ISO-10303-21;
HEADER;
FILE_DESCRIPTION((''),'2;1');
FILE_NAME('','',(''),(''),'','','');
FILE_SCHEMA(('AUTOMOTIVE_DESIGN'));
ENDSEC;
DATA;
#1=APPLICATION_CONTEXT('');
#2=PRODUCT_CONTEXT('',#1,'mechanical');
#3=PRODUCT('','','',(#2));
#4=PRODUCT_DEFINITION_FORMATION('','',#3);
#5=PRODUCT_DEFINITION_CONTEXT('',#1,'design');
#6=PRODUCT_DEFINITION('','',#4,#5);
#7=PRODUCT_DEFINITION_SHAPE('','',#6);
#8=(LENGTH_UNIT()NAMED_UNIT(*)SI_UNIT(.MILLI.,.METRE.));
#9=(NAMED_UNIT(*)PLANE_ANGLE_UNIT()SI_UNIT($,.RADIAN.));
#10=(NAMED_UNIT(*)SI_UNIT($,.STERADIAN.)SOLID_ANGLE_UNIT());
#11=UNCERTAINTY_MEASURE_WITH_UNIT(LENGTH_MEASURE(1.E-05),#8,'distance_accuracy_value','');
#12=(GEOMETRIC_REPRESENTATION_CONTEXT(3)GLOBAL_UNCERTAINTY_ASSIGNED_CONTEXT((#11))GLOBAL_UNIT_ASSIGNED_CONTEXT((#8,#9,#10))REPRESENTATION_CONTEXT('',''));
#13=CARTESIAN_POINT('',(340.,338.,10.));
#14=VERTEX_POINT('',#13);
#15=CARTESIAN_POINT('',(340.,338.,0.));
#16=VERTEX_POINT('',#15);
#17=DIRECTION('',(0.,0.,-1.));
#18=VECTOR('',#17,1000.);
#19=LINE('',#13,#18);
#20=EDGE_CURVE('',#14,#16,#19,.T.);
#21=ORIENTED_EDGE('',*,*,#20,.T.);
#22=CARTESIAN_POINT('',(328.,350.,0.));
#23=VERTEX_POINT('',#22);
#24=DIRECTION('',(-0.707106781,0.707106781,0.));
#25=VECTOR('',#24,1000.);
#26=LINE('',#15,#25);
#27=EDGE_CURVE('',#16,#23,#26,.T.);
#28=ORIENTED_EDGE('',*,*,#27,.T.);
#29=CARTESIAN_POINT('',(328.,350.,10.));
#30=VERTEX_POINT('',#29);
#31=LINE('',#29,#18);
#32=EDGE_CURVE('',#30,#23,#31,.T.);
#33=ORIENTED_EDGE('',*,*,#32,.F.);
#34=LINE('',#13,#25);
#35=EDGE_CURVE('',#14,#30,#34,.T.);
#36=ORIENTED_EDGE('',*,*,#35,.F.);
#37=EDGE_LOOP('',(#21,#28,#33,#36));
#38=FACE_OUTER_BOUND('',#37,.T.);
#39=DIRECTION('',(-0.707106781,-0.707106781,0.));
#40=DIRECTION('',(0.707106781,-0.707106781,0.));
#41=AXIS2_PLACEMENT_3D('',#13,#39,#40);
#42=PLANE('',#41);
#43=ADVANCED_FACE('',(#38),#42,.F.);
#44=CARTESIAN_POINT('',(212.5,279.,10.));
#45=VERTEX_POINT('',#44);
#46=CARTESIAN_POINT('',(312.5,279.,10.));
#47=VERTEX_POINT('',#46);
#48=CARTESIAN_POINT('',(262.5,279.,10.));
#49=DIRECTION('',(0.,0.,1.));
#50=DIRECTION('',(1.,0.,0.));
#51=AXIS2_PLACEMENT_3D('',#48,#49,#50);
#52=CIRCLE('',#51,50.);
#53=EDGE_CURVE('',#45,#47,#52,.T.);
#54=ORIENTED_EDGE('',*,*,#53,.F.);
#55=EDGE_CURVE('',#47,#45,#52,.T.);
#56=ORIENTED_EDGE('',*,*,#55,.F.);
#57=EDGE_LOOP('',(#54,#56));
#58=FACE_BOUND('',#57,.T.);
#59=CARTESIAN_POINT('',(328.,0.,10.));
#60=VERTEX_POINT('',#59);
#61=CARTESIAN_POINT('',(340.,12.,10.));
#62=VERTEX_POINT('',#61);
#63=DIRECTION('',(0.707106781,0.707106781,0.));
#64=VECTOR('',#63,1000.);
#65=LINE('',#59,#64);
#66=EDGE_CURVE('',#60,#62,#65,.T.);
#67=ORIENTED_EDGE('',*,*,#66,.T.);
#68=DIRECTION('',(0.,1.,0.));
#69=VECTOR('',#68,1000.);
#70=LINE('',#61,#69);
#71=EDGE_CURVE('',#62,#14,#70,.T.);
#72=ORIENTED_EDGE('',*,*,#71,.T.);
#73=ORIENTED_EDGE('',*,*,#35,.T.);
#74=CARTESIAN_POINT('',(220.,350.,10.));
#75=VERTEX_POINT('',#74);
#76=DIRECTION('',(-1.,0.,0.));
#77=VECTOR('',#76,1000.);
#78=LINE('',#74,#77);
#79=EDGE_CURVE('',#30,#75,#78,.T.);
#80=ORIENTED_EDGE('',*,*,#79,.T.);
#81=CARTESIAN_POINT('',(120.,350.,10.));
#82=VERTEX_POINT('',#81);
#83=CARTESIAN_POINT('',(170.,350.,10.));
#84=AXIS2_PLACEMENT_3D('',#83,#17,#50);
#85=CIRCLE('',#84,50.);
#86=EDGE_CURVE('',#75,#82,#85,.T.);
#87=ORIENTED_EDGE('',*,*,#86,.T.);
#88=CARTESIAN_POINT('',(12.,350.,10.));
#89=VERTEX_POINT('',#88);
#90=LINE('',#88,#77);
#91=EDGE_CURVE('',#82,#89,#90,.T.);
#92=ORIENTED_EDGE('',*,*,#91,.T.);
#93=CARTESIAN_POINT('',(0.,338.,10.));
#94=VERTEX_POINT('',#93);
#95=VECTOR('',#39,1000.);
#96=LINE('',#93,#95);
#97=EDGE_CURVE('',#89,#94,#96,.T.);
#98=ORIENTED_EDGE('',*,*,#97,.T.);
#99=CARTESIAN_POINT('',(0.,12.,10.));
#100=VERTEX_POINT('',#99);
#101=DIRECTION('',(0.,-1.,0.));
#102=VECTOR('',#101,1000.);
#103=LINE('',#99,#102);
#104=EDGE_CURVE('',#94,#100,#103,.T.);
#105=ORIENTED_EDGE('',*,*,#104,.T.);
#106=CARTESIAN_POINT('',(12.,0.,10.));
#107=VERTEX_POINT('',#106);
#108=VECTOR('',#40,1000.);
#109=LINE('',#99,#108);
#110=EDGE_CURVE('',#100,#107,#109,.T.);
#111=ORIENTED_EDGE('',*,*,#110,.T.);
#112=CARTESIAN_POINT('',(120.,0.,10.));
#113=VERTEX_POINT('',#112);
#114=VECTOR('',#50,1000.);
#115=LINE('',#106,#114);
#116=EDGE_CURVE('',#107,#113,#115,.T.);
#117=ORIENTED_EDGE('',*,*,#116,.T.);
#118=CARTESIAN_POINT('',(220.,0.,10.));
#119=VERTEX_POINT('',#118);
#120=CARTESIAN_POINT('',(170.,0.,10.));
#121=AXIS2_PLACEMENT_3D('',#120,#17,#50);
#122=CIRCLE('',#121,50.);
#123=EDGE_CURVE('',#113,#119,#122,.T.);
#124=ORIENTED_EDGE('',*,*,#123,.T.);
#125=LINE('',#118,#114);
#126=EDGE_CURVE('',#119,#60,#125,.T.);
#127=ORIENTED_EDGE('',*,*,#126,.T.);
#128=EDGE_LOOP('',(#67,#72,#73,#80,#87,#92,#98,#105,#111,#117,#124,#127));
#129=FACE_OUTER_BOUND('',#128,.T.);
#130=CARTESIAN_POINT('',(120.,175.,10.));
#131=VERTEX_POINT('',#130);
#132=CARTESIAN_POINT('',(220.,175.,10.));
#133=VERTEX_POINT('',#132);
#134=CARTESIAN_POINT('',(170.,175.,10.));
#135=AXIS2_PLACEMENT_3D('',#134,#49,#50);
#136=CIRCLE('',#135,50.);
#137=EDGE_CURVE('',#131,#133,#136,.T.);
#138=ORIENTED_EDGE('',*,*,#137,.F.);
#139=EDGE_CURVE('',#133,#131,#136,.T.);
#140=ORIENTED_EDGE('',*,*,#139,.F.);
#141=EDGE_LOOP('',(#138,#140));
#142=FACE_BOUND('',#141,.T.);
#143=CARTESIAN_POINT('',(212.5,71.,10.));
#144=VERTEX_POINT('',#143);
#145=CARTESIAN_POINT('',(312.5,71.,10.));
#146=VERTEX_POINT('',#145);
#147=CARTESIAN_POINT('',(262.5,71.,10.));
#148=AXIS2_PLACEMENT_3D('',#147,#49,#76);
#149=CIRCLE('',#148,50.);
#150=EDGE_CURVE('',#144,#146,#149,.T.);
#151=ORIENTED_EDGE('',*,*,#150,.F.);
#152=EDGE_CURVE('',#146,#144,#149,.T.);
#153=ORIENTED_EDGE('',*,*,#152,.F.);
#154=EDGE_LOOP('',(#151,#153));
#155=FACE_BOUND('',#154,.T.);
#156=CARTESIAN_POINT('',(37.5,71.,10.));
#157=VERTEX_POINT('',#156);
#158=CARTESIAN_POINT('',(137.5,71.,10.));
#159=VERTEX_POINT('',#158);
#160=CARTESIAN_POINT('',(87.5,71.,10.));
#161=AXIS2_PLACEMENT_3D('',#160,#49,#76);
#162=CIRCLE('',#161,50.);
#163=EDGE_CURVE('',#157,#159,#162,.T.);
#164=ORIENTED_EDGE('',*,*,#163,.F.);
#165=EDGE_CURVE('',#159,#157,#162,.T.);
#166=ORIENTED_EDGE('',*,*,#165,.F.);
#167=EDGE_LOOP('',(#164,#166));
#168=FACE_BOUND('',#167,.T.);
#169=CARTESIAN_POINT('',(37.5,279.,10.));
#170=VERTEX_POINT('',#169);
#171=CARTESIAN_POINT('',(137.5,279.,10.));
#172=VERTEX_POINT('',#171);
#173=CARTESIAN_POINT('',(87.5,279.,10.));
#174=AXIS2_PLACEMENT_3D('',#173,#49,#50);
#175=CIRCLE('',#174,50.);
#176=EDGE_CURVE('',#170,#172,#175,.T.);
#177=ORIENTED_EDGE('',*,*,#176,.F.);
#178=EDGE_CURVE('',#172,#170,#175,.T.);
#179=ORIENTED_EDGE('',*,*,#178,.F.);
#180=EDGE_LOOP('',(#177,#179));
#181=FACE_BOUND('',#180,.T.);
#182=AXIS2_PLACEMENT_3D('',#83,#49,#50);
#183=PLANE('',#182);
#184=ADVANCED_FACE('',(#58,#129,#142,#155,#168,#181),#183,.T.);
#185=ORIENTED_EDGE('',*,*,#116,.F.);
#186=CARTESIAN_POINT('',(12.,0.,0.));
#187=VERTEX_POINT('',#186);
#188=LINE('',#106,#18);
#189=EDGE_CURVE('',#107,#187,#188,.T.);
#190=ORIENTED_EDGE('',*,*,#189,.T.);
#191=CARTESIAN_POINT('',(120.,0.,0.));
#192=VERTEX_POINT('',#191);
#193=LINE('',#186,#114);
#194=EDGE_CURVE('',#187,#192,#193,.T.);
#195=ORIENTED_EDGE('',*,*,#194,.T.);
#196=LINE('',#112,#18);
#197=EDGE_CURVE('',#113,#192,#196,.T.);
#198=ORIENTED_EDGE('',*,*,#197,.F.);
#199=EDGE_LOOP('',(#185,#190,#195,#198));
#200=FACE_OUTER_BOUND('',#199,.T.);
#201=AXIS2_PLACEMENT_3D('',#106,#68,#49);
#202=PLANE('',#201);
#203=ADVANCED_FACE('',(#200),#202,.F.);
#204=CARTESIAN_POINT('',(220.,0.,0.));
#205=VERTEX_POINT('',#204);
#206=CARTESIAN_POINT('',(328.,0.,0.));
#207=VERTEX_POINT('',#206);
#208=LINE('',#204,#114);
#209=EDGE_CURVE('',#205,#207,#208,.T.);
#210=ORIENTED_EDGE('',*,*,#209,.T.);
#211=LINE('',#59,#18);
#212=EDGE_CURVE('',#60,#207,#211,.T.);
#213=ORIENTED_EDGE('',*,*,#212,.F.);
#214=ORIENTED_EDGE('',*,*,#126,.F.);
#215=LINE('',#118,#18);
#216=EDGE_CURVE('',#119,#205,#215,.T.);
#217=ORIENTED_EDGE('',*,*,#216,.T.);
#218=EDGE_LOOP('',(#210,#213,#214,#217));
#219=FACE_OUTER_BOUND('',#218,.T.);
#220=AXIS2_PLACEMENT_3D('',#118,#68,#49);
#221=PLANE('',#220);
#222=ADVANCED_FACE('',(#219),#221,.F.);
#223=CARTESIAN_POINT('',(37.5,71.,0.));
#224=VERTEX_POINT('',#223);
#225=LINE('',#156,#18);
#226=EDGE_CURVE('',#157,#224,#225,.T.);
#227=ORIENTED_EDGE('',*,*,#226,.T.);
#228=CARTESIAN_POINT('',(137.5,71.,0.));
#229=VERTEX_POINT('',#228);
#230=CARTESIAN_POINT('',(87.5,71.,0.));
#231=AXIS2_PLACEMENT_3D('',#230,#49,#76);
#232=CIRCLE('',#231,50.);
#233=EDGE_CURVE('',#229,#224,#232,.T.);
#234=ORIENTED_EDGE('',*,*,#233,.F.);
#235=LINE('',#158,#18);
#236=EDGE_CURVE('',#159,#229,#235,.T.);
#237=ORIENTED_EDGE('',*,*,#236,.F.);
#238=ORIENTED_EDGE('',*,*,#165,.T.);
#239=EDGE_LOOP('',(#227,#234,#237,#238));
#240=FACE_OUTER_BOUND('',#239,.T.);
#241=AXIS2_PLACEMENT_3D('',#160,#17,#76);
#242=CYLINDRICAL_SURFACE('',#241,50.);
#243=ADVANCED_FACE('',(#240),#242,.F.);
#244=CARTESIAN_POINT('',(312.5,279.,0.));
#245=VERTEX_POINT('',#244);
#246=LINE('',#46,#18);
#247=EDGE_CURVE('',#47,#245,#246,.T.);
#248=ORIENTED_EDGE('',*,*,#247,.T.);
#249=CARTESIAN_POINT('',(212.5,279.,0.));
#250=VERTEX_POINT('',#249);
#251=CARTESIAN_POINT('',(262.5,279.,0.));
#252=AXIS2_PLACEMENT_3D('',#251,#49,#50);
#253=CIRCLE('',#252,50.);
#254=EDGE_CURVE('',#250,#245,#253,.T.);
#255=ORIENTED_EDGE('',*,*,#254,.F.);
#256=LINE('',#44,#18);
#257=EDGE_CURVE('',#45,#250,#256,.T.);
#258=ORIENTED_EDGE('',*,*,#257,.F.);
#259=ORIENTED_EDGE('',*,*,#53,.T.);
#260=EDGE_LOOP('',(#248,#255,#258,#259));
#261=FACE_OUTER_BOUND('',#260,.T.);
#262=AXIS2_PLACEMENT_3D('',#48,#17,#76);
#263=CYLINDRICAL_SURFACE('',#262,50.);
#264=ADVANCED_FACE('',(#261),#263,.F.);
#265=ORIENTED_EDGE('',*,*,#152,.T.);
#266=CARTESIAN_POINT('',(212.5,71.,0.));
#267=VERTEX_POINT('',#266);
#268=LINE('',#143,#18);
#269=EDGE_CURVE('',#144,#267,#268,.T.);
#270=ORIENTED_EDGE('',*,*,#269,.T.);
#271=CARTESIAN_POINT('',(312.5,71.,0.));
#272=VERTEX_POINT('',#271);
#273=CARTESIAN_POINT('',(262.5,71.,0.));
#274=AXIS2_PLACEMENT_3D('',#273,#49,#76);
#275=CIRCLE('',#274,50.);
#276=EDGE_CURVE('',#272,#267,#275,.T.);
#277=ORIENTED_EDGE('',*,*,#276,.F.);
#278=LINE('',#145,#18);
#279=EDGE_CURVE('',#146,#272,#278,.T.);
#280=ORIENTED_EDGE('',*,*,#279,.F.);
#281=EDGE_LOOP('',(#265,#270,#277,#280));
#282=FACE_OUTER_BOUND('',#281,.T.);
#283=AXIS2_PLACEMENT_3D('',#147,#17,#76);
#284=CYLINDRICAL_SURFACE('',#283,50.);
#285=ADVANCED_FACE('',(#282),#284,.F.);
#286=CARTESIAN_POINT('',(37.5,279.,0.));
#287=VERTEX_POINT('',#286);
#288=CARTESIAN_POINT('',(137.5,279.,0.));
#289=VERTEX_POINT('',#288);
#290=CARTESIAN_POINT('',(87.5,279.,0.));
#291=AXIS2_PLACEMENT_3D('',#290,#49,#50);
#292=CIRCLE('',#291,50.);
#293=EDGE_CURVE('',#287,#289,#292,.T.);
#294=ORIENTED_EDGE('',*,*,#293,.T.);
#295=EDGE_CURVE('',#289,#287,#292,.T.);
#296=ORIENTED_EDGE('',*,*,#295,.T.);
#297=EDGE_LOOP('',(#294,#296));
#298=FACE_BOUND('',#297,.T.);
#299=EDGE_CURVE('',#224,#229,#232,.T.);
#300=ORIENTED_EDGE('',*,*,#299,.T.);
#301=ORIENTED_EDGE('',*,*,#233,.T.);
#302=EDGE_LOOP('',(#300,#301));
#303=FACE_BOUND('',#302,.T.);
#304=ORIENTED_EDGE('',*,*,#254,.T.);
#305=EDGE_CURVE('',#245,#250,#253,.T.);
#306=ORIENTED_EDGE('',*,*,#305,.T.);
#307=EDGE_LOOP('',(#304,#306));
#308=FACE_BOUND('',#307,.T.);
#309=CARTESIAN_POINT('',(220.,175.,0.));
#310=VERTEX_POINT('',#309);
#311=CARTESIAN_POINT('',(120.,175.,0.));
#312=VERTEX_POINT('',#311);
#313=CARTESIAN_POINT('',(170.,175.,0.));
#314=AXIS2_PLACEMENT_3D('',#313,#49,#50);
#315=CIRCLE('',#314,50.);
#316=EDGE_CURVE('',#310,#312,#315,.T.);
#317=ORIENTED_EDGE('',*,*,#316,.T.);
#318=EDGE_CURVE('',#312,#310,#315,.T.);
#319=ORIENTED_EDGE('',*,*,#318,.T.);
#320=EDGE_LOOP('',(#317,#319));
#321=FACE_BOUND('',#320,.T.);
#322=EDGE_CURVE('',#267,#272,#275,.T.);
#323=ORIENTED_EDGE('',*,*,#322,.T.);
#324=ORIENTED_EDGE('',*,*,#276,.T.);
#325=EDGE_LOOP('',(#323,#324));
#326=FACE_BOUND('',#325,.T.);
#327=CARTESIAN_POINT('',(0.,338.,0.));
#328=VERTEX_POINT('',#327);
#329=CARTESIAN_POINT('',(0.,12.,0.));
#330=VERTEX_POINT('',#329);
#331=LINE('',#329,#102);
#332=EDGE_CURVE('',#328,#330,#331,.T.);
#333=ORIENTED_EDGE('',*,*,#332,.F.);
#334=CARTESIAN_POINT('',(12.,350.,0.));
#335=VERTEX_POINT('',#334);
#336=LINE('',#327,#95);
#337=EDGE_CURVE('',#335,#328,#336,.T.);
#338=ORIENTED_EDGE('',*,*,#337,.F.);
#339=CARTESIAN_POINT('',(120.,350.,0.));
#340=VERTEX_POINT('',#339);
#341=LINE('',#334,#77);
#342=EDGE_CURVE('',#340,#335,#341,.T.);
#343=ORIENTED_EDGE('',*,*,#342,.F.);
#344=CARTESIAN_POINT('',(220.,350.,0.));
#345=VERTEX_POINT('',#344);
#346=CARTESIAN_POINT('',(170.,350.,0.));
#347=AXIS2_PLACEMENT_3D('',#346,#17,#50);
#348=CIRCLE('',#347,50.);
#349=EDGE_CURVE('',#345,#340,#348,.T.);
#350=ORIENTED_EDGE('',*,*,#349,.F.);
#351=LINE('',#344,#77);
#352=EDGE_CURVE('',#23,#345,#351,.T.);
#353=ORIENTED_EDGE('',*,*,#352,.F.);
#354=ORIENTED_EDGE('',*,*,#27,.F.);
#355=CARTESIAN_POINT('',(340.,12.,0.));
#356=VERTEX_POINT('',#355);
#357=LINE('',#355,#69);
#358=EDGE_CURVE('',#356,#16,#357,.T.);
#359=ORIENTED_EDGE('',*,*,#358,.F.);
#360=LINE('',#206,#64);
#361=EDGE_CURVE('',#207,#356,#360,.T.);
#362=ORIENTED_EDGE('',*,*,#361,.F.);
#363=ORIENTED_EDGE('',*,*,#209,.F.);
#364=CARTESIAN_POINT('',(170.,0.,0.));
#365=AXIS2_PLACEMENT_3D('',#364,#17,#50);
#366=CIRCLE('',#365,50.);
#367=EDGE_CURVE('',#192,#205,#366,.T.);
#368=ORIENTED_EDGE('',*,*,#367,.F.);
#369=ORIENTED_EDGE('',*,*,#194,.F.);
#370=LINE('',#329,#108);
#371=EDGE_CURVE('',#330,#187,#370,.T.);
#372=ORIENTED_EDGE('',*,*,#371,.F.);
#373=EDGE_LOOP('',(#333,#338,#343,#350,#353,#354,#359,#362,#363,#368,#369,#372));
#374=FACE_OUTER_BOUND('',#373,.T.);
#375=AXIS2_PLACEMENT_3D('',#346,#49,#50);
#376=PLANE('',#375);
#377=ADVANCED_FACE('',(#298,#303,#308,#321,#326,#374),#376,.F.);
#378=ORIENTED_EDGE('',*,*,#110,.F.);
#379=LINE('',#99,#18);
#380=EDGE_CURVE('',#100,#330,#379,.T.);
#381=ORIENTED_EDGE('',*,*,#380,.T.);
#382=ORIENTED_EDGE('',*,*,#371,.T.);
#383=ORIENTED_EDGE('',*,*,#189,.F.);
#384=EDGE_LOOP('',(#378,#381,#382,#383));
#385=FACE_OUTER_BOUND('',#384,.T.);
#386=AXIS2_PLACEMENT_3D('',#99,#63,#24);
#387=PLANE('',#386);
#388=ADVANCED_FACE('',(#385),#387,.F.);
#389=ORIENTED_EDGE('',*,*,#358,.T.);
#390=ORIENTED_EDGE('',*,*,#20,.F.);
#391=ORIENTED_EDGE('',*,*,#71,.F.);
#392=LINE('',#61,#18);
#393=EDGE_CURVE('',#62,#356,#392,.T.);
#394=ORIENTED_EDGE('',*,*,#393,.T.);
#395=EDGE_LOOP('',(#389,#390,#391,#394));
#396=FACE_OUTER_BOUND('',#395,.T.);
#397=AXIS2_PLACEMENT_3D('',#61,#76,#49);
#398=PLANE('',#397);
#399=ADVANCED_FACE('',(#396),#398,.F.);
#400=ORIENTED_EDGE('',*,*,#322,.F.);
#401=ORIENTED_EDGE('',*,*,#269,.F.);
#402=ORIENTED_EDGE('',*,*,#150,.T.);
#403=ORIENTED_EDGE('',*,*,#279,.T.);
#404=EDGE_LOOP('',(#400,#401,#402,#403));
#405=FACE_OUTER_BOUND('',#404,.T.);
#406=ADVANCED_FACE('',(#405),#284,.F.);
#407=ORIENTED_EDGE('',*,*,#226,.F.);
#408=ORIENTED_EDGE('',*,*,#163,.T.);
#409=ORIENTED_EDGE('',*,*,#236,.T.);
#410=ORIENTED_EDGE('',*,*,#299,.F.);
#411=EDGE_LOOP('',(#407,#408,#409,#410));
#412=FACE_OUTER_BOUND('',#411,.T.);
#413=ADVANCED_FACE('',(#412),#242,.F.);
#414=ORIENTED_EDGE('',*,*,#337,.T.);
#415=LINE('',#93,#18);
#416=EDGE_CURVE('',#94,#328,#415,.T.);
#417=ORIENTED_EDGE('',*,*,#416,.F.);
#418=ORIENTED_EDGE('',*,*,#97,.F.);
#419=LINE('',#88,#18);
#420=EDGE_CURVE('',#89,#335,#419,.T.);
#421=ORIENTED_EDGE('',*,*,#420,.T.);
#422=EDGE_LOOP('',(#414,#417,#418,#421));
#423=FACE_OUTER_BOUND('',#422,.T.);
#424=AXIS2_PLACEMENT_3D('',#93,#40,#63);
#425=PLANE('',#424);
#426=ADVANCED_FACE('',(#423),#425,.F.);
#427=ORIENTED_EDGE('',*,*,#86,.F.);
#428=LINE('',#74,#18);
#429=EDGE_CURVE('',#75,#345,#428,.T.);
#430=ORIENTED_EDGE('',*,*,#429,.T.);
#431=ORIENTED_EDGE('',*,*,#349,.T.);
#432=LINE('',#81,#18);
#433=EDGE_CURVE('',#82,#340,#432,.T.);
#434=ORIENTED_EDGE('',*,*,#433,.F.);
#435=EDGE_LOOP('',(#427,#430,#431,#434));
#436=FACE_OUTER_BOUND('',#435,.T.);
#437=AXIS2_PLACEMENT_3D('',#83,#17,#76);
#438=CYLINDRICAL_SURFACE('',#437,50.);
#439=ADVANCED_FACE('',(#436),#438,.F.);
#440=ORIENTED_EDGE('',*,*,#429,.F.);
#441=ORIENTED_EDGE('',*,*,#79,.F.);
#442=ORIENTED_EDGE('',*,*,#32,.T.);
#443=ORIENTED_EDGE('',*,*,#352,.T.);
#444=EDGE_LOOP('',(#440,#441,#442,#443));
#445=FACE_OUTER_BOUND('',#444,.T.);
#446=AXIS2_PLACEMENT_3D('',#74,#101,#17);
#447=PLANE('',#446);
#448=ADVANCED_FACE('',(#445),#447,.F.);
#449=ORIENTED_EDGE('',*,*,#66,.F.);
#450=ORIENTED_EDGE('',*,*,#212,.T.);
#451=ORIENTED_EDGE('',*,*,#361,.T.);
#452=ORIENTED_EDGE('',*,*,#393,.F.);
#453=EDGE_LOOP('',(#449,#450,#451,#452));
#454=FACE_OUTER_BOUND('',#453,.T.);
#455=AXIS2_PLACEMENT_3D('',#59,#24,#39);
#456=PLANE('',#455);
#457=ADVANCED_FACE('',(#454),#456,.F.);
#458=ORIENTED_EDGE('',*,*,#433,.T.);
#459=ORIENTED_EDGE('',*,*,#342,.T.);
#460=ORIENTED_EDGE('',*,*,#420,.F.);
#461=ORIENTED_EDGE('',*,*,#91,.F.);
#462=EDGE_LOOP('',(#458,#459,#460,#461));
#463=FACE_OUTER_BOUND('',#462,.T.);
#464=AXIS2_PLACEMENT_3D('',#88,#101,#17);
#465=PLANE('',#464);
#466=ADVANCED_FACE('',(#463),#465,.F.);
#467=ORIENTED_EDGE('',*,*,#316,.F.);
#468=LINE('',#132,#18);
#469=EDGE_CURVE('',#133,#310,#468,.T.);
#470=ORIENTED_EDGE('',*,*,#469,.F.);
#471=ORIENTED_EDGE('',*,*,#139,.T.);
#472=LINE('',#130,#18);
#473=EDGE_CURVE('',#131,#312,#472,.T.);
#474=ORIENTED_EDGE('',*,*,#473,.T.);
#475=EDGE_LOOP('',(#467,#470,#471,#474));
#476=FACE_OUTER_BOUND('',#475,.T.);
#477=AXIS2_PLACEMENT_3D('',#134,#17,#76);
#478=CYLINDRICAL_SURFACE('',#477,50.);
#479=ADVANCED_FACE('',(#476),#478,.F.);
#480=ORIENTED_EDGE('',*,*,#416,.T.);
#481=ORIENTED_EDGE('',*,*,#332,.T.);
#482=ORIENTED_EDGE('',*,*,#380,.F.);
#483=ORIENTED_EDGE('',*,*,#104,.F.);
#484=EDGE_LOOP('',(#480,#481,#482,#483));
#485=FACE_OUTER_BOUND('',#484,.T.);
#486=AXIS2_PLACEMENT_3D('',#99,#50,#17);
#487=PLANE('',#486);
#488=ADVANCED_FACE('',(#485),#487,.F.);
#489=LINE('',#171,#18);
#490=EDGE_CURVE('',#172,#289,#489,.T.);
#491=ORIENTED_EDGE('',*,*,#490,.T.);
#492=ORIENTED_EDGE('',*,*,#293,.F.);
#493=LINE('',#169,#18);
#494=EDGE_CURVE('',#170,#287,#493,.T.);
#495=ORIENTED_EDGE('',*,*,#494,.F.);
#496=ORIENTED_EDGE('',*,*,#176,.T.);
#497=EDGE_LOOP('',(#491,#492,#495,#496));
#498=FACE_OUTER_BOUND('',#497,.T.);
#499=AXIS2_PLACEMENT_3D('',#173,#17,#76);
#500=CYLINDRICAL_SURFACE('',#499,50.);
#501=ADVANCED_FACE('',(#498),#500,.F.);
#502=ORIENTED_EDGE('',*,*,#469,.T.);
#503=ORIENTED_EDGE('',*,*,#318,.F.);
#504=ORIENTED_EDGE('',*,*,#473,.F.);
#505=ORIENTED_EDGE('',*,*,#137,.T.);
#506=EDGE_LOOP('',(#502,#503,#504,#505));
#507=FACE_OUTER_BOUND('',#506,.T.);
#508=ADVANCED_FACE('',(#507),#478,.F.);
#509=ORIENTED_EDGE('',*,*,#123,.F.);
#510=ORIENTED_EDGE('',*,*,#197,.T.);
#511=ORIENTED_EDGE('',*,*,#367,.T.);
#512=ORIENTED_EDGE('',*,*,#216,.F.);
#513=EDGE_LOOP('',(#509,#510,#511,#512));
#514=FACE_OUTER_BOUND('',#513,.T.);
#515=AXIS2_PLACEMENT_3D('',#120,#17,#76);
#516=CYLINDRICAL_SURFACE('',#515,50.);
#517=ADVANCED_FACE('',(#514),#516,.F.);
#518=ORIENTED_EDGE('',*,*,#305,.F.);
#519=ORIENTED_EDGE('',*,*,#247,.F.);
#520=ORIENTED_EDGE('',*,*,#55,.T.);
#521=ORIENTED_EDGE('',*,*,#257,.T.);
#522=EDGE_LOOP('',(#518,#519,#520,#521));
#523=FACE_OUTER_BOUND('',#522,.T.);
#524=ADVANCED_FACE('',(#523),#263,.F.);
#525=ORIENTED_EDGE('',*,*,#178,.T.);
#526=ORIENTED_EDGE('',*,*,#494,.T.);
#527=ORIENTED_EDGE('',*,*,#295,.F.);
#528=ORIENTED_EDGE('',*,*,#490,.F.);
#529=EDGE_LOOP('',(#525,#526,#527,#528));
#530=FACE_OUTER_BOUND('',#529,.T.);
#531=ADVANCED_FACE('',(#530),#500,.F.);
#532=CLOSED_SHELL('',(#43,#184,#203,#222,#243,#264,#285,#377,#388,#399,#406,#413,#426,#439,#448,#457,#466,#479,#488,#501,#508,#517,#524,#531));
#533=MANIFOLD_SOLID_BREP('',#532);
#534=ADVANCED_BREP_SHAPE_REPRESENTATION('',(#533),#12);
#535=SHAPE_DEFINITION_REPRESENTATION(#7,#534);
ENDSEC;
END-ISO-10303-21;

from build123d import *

# Parameters (mm, degrees)
SKETCH1_R           = 50
BOSS_EXTRUDE1_DEPTH = 10


with BuildPart() as part:
    # Sketch1 → Boss-Extrude1 (new body)
    with BuildSketch(Plane.XY):
        with BuildLine():
            Line((12, 0), (120, 0))
            ThreePointArc((120, 0), (170, 50), (220, 0))
            Line((220, 0), (328, 0))
            Line((328, 0), (340, 12))
            Line((340, 12), (340, 338))
            Line((340, 338), (328, 350))
            Line((328, 350), (220, 350))
            ThreePointArc((220, 350), (170, 300), (120, 350))
            Line((120, 350), (12, 350))
            Line((12, 350), (0, 338))
            Line((0, 338), (0, 12))
            Line((0, 12), (12, 0))
        make_face()
        with Locations((170, 175)):
            Circle(SKETCH1_R, mode=Mode.SUBTRACT)
        with Locations((87.5, 279)):
            Circle(SKETCH1_R, mode=Mode.SUBTRACT)
        with Locations((262.5, 279)):
            Circle(SKETCH1_R, mode=Mode.SUBTRACT)
        with Locations(Location((87.5, 71, 0), (0, 0, 180))):
            Circle(SKETCH1_R, mode=Mode.SUBTRACT)
        with Locations(Location((262.5, 71, 0), (0, 0, 180))):
            Circle(SKETCH1_R, mode=Mode.SUBTRACT)
    extrude(amount=BOSS_EXTRUDE1_DEPTH)


solid = part.part
